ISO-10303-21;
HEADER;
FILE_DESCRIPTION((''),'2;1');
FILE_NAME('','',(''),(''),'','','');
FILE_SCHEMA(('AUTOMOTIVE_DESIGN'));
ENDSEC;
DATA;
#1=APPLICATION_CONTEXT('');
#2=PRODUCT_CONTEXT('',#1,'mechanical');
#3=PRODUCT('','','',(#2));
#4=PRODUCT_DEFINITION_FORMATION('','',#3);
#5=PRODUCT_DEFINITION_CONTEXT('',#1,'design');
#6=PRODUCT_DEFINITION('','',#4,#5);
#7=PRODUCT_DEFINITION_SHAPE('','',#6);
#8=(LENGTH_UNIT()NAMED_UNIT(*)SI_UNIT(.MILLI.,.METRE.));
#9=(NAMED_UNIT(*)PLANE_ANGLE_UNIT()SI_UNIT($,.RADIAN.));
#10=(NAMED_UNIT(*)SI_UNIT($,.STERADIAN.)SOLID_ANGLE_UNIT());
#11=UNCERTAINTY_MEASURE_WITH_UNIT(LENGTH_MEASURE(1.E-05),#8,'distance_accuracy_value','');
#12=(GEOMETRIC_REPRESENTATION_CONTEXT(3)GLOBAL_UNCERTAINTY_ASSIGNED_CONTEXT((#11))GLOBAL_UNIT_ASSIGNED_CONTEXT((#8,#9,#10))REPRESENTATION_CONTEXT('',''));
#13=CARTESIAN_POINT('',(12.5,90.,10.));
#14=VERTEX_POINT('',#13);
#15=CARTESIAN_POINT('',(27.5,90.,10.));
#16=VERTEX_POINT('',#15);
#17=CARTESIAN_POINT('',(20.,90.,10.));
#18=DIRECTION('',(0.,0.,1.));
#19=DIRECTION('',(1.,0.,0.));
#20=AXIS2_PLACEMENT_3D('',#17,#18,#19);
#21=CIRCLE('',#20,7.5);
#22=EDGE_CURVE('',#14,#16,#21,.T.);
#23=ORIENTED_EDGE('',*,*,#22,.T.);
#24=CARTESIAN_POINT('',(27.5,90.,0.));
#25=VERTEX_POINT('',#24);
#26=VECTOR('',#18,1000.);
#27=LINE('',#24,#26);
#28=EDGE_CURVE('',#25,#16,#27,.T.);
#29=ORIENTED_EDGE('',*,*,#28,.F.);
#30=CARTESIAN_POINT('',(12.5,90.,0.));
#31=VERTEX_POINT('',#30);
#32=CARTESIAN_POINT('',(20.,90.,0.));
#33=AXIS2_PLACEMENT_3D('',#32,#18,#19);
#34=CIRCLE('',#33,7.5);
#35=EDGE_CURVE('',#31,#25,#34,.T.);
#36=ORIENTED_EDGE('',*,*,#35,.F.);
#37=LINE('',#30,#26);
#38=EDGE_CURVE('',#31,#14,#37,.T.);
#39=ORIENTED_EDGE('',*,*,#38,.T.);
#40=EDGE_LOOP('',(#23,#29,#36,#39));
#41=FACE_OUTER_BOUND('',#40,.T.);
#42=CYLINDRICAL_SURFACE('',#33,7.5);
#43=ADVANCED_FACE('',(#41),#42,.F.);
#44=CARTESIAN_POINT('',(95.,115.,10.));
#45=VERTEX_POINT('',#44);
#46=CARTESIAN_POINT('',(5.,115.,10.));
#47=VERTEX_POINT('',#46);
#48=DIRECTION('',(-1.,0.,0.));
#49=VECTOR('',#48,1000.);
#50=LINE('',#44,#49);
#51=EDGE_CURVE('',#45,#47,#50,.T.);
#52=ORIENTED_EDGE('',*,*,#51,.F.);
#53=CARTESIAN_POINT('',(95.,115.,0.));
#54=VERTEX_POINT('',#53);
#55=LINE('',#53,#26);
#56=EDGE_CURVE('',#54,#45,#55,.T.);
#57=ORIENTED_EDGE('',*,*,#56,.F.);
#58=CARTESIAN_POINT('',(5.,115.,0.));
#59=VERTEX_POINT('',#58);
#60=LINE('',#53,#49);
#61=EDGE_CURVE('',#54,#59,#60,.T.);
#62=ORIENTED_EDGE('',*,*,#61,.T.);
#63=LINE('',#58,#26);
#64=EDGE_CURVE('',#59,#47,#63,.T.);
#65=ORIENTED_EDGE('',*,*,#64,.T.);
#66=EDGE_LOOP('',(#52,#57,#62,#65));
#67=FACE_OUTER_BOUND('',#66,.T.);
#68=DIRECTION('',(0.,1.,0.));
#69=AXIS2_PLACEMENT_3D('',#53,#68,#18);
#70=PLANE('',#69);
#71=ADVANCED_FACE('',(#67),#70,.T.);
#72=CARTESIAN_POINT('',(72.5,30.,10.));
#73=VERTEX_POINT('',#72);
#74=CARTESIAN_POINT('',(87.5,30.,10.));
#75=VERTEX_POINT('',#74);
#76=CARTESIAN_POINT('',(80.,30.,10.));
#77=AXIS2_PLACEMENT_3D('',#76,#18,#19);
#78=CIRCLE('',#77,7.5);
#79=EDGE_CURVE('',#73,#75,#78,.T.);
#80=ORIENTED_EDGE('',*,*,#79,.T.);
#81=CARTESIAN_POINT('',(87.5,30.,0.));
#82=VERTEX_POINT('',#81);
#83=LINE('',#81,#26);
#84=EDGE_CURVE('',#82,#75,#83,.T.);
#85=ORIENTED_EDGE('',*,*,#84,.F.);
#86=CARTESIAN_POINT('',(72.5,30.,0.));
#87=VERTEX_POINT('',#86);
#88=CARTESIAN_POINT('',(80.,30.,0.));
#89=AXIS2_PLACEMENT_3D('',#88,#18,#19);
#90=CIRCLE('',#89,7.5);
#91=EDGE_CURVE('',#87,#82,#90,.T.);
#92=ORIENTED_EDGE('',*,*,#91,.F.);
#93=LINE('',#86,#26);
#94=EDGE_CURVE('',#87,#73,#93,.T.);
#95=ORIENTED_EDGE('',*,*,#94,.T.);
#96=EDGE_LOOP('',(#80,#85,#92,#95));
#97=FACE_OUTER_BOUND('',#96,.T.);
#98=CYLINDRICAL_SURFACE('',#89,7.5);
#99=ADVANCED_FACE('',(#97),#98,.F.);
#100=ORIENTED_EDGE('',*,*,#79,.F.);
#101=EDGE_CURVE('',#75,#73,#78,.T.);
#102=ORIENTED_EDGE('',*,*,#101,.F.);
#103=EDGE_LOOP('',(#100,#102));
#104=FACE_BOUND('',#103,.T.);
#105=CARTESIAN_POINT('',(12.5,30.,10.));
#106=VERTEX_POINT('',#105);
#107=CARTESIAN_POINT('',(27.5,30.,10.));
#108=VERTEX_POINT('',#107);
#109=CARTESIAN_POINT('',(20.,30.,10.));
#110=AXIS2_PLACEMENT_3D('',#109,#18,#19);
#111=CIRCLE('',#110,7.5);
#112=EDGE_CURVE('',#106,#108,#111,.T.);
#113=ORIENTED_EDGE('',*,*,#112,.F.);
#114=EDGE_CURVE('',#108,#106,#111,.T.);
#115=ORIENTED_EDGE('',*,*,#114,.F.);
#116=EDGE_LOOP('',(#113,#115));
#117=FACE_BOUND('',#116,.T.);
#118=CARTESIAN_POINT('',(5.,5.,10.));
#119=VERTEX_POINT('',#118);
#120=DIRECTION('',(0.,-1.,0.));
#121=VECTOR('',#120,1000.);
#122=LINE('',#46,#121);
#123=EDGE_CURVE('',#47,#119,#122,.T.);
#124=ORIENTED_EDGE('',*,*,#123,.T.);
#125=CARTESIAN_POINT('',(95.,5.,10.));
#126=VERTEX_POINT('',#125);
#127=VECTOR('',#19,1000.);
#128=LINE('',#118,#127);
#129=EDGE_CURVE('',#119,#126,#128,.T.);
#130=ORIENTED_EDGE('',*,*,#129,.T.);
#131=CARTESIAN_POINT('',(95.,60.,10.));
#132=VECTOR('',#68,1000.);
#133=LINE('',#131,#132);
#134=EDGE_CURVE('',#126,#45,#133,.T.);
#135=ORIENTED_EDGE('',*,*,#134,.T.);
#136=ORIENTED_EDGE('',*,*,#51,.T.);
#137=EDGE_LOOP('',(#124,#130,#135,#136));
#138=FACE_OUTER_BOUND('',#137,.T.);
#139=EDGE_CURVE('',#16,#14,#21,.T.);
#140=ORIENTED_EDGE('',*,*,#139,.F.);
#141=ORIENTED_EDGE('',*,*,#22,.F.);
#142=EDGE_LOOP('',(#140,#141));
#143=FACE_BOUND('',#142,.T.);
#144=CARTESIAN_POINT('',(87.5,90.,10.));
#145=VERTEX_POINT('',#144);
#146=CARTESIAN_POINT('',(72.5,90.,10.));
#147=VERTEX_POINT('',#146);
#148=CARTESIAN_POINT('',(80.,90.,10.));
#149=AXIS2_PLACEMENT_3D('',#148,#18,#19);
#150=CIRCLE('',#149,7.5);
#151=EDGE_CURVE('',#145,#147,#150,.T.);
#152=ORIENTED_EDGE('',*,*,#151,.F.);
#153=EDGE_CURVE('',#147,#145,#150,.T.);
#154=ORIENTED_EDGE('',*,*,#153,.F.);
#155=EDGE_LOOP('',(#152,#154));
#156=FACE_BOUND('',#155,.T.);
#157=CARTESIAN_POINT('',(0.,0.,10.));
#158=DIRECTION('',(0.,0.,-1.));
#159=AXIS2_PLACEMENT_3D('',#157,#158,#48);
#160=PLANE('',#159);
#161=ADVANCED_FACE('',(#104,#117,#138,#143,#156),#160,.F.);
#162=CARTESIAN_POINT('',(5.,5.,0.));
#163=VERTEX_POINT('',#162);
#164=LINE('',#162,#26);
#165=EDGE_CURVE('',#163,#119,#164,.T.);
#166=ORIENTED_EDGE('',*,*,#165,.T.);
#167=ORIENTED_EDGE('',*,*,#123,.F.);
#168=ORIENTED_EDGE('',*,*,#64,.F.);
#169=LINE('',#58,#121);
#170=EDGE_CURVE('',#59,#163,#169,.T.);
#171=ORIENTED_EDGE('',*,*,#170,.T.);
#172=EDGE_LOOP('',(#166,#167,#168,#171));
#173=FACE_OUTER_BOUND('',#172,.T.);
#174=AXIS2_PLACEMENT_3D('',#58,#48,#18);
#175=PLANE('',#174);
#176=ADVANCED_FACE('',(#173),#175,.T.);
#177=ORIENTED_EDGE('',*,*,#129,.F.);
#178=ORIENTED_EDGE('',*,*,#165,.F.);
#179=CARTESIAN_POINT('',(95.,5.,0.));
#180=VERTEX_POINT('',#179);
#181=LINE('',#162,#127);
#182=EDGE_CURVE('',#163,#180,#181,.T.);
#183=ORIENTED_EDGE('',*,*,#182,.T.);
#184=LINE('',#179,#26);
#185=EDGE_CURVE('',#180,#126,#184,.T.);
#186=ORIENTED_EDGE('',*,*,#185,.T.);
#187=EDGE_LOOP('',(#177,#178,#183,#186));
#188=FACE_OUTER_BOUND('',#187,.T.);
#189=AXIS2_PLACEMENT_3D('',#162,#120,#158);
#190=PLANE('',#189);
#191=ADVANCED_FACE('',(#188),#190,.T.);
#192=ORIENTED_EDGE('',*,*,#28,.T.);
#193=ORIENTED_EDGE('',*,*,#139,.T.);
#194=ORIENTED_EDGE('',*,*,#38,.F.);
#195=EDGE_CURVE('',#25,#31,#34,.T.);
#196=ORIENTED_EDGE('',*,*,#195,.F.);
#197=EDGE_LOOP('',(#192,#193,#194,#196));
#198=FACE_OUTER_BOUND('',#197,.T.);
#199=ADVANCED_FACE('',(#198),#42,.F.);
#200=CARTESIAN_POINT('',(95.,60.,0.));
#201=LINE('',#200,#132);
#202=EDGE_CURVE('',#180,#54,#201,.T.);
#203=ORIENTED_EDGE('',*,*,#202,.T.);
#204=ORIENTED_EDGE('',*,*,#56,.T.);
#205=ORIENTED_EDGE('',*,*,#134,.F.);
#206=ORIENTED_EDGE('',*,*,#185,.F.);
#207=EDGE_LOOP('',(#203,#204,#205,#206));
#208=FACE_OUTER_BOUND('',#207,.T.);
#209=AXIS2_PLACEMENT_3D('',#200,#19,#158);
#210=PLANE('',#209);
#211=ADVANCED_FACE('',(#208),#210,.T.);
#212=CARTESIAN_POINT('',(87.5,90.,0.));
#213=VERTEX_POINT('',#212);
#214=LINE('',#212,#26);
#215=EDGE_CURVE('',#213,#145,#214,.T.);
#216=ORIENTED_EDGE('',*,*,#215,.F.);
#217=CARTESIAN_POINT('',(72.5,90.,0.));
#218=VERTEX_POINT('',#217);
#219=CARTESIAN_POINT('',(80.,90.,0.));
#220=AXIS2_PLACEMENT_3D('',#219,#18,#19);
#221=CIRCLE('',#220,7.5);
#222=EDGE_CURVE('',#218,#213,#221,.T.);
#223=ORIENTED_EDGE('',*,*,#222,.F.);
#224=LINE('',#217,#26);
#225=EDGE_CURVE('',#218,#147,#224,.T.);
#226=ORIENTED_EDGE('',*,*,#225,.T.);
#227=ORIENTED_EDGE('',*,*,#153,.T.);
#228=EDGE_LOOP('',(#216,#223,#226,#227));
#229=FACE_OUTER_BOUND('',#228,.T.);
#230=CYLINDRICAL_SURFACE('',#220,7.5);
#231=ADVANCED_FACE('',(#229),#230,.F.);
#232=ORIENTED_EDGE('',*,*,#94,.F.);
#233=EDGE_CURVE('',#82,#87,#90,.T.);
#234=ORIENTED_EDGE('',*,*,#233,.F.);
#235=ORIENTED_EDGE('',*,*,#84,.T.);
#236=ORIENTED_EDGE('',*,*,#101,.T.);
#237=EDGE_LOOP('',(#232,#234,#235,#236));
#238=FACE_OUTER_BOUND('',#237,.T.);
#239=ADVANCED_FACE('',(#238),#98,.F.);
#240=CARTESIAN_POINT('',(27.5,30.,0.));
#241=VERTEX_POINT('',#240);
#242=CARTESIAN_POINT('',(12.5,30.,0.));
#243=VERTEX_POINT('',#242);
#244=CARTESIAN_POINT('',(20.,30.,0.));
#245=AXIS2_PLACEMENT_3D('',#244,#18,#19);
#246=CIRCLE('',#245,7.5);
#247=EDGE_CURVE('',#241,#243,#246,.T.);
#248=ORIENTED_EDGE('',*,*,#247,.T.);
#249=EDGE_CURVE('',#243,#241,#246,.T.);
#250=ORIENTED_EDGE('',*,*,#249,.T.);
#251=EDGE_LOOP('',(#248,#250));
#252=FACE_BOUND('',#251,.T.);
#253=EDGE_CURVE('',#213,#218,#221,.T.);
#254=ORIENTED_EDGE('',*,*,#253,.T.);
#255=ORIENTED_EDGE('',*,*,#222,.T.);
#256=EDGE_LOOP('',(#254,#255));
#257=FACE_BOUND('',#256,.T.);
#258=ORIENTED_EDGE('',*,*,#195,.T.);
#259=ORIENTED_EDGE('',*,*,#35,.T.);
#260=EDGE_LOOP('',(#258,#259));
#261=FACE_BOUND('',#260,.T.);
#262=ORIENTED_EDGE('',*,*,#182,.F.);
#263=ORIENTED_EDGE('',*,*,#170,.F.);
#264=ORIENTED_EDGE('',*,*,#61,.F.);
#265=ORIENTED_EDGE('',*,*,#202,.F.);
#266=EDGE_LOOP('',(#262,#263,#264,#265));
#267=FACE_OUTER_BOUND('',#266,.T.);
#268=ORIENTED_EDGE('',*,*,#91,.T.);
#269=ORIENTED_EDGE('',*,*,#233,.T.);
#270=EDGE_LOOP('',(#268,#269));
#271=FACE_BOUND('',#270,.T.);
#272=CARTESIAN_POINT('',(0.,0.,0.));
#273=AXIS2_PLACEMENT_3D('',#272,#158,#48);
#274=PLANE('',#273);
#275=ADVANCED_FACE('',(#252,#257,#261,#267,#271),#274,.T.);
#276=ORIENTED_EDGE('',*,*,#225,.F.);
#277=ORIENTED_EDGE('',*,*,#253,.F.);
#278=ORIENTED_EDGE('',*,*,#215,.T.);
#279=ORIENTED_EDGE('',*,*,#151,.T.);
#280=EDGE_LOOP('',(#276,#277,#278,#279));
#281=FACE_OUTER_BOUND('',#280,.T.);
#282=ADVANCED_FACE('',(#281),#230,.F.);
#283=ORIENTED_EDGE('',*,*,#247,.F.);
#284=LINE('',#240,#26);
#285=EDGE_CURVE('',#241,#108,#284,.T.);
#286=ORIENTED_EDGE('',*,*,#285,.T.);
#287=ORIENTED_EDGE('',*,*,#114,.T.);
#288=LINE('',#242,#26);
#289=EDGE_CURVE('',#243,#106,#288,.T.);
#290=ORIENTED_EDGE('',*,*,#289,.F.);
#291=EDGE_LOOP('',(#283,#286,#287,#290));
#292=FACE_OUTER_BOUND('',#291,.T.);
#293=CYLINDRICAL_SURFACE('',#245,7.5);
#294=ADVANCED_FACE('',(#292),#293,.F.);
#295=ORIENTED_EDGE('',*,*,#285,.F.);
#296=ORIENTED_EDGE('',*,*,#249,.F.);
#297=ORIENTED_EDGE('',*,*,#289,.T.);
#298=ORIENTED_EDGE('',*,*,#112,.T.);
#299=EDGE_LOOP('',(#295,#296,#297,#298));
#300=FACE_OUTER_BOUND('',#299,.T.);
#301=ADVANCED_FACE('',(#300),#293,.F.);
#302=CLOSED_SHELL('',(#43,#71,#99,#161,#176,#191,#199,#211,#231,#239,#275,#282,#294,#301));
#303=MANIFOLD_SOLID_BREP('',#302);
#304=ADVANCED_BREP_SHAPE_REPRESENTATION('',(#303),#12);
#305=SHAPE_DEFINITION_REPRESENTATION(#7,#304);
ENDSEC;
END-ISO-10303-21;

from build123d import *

# Parameters (mm, degrees)
SKETCH_1_W          = 100
SKETCH_1_H          = 120
EXTRUDE_1_DEPTH     = 10
CUT_EXTRUDE_1_DEPTH = 10
SKETCH_3_W          = 100
SKETCH_3_H          = 120
CUT_EXTRUDE_2_DEPTH = 10


with BuildPart() as part:
    # 草图1 → 凸台-拉伸1 (new body)
    with BuildSketch(Plane.XY):
        with Locations((50, 60)):
            Rectangle(SKETCH_1_W, SKETCH_1_H)
    extrude(amount=EXTRUDE_1_DEPTH)

    # 草图2 → 切除-拉伸1 (cut)
    with BuildSketch(Plane.XY.offset(10)):
        with BuildLine():
            ThreePointArc((87.5, 90), (80, 97.5), (72.5, 90))
            Line((72.5, 90), (80, 90))
            Line((80, 90), (80, 82.5))
            ThreePointArc((80, 82.5), (85.303300859, 84.696699141), (87.5, 90))
        make_face()
        with BuildLine():
            Line((80, 90), (72.5, 90))
            ThreePointArc((72.5, 90), (74.696699141, 84.696699141), (80, 82.5))
            Line((80, 82.5), (80, 90))
        make_face()
        with BuildLine():
            ThreePointArc((27.5, 90), (14.696699141, 95.303300859), (20, 82.5))
            Line((20, 82.5), (20, 90))
            Line((20, 90), (27.5, 90))
        make_face()
        with BuildLine():
            Line((20, 90), (20, 82.5))
            ThreePointArc((20, 82.5), (25.303300859, 84.696699141), (27.5, 90))
            Line((27.5, 90), (20, 90))
        make_face()
        with BuildLine():
            ThreePointArc((27.5, 30), (25.303300859, 35.303300859), (20, 37.5))
            Line((20, 37.5), (20, 30))
            Line((20, 30), (27.5, 30))
        make_face()
        with BuildLine():
            Line((20, 30), (20, 37.5))
            ThreePointArc((20, 37.5), (14.696699141, 24.696699141), (27.5, 30))
            Line((27.5, 30), (20, 30))
        make_face()
        with BuildLine():
            ThreePointArc((80, 37.5), (74.696699141, 35.303300859), (72.5, 30))
            Line((72.5, 30), (80, 30))
            Line((80, 30), (80, 37.5))
        make_face()
        with BuildLine():
            Line((80, 30), (72.5, 30))
            ThreePointArc((72.5, 30), (80, 22.5), (87.5, 30))
            ThreePointArc((87.5, 30), (85.303300859, 35.303300859), (80, 37.5))
            Line((80, 37.5), (80, 30))
        make_face()
    extrude(amount=-CUT_EXTRUDE_1_DEPTH, mode=Mode.SUBTRACT)

    # 草图3 → 切除-拉伸2 (cut)
    with BuildSketch(Plane.XY.offset(10)):
        with Locations((50, 60)):
            Rectangle(SKETCH_3_W, SKETCH_3_H)
        Polygon((95, 60), (95, 5), (5, 5), (5, 115), (95, 115), align=None, mode=Mode.SUBTRACT)
    extrude(amount=-CUT_EXTRUDE_2_DEPTH, mode=Mode.SUBTRACT)


solid = part.part
